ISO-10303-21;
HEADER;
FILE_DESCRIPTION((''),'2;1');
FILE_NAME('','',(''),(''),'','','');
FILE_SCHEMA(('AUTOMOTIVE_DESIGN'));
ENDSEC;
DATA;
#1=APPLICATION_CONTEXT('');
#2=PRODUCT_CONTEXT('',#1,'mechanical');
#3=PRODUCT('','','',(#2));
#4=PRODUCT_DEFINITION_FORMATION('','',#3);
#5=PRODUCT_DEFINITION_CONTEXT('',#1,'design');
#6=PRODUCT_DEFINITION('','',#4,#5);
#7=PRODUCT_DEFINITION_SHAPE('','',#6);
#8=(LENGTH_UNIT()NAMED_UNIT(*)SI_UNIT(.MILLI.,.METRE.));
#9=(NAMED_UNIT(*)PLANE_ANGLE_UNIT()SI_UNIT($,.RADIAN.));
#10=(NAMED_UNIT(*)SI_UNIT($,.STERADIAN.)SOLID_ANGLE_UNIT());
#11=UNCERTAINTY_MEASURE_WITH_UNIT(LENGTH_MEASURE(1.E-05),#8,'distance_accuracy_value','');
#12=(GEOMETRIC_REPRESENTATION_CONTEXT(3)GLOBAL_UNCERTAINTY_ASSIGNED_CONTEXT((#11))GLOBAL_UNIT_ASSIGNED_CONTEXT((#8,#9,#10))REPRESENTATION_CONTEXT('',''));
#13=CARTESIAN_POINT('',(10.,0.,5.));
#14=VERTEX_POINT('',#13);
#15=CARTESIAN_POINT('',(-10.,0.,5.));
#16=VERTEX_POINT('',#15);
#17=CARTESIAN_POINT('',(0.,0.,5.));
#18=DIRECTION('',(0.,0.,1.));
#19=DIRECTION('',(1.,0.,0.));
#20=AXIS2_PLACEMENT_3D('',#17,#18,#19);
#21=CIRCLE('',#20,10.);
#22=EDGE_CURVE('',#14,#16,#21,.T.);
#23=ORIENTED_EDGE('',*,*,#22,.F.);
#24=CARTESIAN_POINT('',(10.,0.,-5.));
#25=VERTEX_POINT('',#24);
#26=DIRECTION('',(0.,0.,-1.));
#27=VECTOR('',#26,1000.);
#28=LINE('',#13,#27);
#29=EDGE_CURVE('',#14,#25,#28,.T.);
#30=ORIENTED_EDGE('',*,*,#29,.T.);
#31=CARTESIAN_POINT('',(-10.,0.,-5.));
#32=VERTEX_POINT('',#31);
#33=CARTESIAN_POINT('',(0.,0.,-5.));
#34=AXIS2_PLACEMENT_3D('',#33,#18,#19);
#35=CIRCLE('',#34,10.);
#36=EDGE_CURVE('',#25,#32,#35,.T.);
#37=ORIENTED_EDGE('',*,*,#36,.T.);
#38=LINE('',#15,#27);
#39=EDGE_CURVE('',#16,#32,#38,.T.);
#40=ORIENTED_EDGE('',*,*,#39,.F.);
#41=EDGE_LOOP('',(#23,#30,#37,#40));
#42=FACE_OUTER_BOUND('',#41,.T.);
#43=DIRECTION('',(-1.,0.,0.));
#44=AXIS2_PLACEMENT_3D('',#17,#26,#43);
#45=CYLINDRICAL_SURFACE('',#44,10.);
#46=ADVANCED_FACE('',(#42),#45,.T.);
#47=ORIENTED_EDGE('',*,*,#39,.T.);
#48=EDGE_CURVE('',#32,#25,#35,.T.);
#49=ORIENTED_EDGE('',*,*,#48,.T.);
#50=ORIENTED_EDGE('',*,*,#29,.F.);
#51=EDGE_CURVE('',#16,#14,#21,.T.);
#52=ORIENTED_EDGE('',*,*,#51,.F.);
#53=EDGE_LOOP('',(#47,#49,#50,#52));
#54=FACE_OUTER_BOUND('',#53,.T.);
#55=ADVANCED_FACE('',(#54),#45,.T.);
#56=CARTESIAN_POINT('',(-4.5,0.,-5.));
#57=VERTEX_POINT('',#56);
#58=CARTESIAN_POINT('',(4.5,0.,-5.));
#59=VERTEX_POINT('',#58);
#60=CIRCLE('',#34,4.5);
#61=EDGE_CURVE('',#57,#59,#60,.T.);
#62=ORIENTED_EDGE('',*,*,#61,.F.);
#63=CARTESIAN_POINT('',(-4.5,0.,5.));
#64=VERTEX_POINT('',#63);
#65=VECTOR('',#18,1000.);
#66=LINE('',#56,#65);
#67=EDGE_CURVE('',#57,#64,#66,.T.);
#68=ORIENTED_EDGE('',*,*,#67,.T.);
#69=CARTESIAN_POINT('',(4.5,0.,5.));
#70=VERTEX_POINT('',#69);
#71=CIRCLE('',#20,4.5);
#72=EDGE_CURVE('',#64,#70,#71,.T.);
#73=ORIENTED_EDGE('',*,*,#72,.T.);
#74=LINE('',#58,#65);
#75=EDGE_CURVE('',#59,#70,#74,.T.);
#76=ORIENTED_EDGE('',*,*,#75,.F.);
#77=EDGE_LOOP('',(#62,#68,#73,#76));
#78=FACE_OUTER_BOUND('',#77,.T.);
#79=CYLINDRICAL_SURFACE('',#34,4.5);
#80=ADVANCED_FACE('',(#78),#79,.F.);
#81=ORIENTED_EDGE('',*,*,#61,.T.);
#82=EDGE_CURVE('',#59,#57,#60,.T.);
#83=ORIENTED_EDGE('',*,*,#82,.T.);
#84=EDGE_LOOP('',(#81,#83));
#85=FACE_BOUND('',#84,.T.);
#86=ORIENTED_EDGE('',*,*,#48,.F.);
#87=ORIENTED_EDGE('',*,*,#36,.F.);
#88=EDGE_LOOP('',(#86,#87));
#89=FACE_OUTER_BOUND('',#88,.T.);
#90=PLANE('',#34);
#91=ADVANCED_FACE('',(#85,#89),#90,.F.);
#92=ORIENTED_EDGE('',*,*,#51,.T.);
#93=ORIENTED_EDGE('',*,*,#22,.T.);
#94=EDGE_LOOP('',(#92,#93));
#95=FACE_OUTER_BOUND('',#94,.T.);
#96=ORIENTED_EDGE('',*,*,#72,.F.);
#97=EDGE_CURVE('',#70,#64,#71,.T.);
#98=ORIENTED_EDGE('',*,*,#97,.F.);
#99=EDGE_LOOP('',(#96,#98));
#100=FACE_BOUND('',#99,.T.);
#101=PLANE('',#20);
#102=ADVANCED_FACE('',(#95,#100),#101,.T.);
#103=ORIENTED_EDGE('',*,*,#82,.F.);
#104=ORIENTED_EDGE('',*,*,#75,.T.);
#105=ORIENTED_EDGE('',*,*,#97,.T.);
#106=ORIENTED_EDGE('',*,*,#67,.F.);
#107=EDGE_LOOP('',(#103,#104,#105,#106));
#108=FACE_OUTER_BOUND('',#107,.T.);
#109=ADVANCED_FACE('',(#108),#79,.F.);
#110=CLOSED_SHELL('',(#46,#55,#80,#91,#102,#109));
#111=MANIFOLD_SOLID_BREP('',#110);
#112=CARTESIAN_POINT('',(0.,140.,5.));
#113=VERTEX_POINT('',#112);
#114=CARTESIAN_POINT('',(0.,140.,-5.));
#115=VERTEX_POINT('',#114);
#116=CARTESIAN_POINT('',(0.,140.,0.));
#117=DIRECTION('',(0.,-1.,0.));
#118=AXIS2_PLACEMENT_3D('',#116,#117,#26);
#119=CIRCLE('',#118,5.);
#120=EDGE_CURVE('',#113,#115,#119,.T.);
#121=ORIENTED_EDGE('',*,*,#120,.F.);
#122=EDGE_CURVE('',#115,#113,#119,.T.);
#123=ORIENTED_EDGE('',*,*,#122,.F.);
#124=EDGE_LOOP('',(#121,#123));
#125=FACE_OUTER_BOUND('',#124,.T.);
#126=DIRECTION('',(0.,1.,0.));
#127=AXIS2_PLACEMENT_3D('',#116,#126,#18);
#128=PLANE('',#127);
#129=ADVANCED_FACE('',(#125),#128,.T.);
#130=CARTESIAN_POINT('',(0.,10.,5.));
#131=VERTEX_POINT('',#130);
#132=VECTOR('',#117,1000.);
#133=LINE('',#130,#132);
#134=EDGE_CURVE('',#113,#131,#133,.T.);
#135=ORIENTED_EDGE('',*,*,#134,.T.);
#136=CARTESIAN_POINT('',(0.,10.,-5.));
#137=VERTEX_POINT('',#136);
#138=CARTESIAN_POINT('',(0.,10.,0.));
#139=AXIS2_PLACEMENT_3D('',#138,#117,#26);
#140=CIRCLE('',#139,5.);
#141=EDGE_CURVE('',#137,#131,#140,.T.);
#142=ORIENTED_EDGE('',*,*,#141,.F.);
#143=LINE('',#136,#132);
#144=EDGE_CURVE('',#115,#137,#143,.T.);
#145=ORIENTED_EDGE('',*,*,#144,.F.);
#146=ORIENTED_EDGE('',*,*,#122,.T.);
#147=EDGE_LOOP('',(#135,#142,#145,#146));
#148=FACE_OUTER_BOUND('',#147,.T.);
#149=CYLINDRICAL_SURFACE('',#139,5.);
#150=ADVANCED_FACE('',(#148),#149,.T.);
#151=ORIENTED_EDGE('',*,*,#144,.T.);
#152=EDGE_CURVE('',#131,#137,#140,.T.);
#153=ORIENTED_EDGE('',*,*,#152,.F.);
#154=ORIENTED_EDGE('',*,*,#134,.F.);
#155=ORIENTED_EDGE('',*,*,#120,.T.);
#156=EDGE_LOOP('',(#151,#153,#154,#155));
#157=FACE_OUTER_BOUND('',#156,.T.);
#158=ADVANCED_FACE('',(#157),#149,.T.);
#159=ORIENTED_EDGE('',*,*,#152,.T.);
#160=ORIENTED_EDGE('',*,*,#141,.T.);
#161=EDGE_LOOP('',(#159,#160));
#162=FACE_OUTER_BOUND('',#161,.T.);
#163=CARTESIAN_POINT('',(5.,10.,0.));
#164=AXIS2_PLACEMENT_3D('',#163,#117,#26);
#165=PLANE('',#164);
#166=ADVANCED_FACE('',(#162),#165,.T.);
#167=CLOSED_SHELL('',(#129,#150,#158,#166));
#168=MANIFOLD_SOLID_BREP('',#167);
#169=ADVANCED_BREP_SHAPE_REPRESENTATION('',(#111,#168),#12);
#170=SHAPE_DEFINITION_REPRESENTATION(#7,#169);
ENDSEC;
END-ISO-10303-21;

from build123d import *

# Parameters (mm, degrees)
SKETCH1_R           = 10
BOSS_EXTRUDE1_DEPTH = 5
SKETCH2_R           = 4.5
CUT_EXTRUDE1_DEPTH  = 10
SKETCH4_W           = 5
SKETCH4_H           = 130


with BuildPart() as part:
    # Sketch1 → Boss-Extrude1 (new, symmetric)
    with BuildSketch(Plane.XY):
        Circle(SKETCH1_R)
    extrude(amount=BOSS_EXTRUDE1_DEPTH, both=True)

    # Sketch2 → Cut-Extrude1 (cut)
    with BuildSketch(Plane.XY.offset(5)):
        Circle(SKETCH2_R)
    extrude(amount=-CUT_EXTRUDE1_DEPTH, mode=Mode.SUBTRACT)


with BuildPart() as body_2:
    # Sketch4 → Revolve1 (revolve)
    with BuildSketch(Plane.XY, mode=Mode.PRIVATE) as revolve1_sk:
        with Locations((2.5, 75)):
            Rectangle(SKETCH4_W, SKETCH4_H)
    revolve(revolve1_sk.sketch.rotate(Axis((0, 10, 0), (0, 1, 0)), 90), axis=Axis((0, 10, 0), (0, 1, 0)))


solid = Compound([part.part, body_2.part])
